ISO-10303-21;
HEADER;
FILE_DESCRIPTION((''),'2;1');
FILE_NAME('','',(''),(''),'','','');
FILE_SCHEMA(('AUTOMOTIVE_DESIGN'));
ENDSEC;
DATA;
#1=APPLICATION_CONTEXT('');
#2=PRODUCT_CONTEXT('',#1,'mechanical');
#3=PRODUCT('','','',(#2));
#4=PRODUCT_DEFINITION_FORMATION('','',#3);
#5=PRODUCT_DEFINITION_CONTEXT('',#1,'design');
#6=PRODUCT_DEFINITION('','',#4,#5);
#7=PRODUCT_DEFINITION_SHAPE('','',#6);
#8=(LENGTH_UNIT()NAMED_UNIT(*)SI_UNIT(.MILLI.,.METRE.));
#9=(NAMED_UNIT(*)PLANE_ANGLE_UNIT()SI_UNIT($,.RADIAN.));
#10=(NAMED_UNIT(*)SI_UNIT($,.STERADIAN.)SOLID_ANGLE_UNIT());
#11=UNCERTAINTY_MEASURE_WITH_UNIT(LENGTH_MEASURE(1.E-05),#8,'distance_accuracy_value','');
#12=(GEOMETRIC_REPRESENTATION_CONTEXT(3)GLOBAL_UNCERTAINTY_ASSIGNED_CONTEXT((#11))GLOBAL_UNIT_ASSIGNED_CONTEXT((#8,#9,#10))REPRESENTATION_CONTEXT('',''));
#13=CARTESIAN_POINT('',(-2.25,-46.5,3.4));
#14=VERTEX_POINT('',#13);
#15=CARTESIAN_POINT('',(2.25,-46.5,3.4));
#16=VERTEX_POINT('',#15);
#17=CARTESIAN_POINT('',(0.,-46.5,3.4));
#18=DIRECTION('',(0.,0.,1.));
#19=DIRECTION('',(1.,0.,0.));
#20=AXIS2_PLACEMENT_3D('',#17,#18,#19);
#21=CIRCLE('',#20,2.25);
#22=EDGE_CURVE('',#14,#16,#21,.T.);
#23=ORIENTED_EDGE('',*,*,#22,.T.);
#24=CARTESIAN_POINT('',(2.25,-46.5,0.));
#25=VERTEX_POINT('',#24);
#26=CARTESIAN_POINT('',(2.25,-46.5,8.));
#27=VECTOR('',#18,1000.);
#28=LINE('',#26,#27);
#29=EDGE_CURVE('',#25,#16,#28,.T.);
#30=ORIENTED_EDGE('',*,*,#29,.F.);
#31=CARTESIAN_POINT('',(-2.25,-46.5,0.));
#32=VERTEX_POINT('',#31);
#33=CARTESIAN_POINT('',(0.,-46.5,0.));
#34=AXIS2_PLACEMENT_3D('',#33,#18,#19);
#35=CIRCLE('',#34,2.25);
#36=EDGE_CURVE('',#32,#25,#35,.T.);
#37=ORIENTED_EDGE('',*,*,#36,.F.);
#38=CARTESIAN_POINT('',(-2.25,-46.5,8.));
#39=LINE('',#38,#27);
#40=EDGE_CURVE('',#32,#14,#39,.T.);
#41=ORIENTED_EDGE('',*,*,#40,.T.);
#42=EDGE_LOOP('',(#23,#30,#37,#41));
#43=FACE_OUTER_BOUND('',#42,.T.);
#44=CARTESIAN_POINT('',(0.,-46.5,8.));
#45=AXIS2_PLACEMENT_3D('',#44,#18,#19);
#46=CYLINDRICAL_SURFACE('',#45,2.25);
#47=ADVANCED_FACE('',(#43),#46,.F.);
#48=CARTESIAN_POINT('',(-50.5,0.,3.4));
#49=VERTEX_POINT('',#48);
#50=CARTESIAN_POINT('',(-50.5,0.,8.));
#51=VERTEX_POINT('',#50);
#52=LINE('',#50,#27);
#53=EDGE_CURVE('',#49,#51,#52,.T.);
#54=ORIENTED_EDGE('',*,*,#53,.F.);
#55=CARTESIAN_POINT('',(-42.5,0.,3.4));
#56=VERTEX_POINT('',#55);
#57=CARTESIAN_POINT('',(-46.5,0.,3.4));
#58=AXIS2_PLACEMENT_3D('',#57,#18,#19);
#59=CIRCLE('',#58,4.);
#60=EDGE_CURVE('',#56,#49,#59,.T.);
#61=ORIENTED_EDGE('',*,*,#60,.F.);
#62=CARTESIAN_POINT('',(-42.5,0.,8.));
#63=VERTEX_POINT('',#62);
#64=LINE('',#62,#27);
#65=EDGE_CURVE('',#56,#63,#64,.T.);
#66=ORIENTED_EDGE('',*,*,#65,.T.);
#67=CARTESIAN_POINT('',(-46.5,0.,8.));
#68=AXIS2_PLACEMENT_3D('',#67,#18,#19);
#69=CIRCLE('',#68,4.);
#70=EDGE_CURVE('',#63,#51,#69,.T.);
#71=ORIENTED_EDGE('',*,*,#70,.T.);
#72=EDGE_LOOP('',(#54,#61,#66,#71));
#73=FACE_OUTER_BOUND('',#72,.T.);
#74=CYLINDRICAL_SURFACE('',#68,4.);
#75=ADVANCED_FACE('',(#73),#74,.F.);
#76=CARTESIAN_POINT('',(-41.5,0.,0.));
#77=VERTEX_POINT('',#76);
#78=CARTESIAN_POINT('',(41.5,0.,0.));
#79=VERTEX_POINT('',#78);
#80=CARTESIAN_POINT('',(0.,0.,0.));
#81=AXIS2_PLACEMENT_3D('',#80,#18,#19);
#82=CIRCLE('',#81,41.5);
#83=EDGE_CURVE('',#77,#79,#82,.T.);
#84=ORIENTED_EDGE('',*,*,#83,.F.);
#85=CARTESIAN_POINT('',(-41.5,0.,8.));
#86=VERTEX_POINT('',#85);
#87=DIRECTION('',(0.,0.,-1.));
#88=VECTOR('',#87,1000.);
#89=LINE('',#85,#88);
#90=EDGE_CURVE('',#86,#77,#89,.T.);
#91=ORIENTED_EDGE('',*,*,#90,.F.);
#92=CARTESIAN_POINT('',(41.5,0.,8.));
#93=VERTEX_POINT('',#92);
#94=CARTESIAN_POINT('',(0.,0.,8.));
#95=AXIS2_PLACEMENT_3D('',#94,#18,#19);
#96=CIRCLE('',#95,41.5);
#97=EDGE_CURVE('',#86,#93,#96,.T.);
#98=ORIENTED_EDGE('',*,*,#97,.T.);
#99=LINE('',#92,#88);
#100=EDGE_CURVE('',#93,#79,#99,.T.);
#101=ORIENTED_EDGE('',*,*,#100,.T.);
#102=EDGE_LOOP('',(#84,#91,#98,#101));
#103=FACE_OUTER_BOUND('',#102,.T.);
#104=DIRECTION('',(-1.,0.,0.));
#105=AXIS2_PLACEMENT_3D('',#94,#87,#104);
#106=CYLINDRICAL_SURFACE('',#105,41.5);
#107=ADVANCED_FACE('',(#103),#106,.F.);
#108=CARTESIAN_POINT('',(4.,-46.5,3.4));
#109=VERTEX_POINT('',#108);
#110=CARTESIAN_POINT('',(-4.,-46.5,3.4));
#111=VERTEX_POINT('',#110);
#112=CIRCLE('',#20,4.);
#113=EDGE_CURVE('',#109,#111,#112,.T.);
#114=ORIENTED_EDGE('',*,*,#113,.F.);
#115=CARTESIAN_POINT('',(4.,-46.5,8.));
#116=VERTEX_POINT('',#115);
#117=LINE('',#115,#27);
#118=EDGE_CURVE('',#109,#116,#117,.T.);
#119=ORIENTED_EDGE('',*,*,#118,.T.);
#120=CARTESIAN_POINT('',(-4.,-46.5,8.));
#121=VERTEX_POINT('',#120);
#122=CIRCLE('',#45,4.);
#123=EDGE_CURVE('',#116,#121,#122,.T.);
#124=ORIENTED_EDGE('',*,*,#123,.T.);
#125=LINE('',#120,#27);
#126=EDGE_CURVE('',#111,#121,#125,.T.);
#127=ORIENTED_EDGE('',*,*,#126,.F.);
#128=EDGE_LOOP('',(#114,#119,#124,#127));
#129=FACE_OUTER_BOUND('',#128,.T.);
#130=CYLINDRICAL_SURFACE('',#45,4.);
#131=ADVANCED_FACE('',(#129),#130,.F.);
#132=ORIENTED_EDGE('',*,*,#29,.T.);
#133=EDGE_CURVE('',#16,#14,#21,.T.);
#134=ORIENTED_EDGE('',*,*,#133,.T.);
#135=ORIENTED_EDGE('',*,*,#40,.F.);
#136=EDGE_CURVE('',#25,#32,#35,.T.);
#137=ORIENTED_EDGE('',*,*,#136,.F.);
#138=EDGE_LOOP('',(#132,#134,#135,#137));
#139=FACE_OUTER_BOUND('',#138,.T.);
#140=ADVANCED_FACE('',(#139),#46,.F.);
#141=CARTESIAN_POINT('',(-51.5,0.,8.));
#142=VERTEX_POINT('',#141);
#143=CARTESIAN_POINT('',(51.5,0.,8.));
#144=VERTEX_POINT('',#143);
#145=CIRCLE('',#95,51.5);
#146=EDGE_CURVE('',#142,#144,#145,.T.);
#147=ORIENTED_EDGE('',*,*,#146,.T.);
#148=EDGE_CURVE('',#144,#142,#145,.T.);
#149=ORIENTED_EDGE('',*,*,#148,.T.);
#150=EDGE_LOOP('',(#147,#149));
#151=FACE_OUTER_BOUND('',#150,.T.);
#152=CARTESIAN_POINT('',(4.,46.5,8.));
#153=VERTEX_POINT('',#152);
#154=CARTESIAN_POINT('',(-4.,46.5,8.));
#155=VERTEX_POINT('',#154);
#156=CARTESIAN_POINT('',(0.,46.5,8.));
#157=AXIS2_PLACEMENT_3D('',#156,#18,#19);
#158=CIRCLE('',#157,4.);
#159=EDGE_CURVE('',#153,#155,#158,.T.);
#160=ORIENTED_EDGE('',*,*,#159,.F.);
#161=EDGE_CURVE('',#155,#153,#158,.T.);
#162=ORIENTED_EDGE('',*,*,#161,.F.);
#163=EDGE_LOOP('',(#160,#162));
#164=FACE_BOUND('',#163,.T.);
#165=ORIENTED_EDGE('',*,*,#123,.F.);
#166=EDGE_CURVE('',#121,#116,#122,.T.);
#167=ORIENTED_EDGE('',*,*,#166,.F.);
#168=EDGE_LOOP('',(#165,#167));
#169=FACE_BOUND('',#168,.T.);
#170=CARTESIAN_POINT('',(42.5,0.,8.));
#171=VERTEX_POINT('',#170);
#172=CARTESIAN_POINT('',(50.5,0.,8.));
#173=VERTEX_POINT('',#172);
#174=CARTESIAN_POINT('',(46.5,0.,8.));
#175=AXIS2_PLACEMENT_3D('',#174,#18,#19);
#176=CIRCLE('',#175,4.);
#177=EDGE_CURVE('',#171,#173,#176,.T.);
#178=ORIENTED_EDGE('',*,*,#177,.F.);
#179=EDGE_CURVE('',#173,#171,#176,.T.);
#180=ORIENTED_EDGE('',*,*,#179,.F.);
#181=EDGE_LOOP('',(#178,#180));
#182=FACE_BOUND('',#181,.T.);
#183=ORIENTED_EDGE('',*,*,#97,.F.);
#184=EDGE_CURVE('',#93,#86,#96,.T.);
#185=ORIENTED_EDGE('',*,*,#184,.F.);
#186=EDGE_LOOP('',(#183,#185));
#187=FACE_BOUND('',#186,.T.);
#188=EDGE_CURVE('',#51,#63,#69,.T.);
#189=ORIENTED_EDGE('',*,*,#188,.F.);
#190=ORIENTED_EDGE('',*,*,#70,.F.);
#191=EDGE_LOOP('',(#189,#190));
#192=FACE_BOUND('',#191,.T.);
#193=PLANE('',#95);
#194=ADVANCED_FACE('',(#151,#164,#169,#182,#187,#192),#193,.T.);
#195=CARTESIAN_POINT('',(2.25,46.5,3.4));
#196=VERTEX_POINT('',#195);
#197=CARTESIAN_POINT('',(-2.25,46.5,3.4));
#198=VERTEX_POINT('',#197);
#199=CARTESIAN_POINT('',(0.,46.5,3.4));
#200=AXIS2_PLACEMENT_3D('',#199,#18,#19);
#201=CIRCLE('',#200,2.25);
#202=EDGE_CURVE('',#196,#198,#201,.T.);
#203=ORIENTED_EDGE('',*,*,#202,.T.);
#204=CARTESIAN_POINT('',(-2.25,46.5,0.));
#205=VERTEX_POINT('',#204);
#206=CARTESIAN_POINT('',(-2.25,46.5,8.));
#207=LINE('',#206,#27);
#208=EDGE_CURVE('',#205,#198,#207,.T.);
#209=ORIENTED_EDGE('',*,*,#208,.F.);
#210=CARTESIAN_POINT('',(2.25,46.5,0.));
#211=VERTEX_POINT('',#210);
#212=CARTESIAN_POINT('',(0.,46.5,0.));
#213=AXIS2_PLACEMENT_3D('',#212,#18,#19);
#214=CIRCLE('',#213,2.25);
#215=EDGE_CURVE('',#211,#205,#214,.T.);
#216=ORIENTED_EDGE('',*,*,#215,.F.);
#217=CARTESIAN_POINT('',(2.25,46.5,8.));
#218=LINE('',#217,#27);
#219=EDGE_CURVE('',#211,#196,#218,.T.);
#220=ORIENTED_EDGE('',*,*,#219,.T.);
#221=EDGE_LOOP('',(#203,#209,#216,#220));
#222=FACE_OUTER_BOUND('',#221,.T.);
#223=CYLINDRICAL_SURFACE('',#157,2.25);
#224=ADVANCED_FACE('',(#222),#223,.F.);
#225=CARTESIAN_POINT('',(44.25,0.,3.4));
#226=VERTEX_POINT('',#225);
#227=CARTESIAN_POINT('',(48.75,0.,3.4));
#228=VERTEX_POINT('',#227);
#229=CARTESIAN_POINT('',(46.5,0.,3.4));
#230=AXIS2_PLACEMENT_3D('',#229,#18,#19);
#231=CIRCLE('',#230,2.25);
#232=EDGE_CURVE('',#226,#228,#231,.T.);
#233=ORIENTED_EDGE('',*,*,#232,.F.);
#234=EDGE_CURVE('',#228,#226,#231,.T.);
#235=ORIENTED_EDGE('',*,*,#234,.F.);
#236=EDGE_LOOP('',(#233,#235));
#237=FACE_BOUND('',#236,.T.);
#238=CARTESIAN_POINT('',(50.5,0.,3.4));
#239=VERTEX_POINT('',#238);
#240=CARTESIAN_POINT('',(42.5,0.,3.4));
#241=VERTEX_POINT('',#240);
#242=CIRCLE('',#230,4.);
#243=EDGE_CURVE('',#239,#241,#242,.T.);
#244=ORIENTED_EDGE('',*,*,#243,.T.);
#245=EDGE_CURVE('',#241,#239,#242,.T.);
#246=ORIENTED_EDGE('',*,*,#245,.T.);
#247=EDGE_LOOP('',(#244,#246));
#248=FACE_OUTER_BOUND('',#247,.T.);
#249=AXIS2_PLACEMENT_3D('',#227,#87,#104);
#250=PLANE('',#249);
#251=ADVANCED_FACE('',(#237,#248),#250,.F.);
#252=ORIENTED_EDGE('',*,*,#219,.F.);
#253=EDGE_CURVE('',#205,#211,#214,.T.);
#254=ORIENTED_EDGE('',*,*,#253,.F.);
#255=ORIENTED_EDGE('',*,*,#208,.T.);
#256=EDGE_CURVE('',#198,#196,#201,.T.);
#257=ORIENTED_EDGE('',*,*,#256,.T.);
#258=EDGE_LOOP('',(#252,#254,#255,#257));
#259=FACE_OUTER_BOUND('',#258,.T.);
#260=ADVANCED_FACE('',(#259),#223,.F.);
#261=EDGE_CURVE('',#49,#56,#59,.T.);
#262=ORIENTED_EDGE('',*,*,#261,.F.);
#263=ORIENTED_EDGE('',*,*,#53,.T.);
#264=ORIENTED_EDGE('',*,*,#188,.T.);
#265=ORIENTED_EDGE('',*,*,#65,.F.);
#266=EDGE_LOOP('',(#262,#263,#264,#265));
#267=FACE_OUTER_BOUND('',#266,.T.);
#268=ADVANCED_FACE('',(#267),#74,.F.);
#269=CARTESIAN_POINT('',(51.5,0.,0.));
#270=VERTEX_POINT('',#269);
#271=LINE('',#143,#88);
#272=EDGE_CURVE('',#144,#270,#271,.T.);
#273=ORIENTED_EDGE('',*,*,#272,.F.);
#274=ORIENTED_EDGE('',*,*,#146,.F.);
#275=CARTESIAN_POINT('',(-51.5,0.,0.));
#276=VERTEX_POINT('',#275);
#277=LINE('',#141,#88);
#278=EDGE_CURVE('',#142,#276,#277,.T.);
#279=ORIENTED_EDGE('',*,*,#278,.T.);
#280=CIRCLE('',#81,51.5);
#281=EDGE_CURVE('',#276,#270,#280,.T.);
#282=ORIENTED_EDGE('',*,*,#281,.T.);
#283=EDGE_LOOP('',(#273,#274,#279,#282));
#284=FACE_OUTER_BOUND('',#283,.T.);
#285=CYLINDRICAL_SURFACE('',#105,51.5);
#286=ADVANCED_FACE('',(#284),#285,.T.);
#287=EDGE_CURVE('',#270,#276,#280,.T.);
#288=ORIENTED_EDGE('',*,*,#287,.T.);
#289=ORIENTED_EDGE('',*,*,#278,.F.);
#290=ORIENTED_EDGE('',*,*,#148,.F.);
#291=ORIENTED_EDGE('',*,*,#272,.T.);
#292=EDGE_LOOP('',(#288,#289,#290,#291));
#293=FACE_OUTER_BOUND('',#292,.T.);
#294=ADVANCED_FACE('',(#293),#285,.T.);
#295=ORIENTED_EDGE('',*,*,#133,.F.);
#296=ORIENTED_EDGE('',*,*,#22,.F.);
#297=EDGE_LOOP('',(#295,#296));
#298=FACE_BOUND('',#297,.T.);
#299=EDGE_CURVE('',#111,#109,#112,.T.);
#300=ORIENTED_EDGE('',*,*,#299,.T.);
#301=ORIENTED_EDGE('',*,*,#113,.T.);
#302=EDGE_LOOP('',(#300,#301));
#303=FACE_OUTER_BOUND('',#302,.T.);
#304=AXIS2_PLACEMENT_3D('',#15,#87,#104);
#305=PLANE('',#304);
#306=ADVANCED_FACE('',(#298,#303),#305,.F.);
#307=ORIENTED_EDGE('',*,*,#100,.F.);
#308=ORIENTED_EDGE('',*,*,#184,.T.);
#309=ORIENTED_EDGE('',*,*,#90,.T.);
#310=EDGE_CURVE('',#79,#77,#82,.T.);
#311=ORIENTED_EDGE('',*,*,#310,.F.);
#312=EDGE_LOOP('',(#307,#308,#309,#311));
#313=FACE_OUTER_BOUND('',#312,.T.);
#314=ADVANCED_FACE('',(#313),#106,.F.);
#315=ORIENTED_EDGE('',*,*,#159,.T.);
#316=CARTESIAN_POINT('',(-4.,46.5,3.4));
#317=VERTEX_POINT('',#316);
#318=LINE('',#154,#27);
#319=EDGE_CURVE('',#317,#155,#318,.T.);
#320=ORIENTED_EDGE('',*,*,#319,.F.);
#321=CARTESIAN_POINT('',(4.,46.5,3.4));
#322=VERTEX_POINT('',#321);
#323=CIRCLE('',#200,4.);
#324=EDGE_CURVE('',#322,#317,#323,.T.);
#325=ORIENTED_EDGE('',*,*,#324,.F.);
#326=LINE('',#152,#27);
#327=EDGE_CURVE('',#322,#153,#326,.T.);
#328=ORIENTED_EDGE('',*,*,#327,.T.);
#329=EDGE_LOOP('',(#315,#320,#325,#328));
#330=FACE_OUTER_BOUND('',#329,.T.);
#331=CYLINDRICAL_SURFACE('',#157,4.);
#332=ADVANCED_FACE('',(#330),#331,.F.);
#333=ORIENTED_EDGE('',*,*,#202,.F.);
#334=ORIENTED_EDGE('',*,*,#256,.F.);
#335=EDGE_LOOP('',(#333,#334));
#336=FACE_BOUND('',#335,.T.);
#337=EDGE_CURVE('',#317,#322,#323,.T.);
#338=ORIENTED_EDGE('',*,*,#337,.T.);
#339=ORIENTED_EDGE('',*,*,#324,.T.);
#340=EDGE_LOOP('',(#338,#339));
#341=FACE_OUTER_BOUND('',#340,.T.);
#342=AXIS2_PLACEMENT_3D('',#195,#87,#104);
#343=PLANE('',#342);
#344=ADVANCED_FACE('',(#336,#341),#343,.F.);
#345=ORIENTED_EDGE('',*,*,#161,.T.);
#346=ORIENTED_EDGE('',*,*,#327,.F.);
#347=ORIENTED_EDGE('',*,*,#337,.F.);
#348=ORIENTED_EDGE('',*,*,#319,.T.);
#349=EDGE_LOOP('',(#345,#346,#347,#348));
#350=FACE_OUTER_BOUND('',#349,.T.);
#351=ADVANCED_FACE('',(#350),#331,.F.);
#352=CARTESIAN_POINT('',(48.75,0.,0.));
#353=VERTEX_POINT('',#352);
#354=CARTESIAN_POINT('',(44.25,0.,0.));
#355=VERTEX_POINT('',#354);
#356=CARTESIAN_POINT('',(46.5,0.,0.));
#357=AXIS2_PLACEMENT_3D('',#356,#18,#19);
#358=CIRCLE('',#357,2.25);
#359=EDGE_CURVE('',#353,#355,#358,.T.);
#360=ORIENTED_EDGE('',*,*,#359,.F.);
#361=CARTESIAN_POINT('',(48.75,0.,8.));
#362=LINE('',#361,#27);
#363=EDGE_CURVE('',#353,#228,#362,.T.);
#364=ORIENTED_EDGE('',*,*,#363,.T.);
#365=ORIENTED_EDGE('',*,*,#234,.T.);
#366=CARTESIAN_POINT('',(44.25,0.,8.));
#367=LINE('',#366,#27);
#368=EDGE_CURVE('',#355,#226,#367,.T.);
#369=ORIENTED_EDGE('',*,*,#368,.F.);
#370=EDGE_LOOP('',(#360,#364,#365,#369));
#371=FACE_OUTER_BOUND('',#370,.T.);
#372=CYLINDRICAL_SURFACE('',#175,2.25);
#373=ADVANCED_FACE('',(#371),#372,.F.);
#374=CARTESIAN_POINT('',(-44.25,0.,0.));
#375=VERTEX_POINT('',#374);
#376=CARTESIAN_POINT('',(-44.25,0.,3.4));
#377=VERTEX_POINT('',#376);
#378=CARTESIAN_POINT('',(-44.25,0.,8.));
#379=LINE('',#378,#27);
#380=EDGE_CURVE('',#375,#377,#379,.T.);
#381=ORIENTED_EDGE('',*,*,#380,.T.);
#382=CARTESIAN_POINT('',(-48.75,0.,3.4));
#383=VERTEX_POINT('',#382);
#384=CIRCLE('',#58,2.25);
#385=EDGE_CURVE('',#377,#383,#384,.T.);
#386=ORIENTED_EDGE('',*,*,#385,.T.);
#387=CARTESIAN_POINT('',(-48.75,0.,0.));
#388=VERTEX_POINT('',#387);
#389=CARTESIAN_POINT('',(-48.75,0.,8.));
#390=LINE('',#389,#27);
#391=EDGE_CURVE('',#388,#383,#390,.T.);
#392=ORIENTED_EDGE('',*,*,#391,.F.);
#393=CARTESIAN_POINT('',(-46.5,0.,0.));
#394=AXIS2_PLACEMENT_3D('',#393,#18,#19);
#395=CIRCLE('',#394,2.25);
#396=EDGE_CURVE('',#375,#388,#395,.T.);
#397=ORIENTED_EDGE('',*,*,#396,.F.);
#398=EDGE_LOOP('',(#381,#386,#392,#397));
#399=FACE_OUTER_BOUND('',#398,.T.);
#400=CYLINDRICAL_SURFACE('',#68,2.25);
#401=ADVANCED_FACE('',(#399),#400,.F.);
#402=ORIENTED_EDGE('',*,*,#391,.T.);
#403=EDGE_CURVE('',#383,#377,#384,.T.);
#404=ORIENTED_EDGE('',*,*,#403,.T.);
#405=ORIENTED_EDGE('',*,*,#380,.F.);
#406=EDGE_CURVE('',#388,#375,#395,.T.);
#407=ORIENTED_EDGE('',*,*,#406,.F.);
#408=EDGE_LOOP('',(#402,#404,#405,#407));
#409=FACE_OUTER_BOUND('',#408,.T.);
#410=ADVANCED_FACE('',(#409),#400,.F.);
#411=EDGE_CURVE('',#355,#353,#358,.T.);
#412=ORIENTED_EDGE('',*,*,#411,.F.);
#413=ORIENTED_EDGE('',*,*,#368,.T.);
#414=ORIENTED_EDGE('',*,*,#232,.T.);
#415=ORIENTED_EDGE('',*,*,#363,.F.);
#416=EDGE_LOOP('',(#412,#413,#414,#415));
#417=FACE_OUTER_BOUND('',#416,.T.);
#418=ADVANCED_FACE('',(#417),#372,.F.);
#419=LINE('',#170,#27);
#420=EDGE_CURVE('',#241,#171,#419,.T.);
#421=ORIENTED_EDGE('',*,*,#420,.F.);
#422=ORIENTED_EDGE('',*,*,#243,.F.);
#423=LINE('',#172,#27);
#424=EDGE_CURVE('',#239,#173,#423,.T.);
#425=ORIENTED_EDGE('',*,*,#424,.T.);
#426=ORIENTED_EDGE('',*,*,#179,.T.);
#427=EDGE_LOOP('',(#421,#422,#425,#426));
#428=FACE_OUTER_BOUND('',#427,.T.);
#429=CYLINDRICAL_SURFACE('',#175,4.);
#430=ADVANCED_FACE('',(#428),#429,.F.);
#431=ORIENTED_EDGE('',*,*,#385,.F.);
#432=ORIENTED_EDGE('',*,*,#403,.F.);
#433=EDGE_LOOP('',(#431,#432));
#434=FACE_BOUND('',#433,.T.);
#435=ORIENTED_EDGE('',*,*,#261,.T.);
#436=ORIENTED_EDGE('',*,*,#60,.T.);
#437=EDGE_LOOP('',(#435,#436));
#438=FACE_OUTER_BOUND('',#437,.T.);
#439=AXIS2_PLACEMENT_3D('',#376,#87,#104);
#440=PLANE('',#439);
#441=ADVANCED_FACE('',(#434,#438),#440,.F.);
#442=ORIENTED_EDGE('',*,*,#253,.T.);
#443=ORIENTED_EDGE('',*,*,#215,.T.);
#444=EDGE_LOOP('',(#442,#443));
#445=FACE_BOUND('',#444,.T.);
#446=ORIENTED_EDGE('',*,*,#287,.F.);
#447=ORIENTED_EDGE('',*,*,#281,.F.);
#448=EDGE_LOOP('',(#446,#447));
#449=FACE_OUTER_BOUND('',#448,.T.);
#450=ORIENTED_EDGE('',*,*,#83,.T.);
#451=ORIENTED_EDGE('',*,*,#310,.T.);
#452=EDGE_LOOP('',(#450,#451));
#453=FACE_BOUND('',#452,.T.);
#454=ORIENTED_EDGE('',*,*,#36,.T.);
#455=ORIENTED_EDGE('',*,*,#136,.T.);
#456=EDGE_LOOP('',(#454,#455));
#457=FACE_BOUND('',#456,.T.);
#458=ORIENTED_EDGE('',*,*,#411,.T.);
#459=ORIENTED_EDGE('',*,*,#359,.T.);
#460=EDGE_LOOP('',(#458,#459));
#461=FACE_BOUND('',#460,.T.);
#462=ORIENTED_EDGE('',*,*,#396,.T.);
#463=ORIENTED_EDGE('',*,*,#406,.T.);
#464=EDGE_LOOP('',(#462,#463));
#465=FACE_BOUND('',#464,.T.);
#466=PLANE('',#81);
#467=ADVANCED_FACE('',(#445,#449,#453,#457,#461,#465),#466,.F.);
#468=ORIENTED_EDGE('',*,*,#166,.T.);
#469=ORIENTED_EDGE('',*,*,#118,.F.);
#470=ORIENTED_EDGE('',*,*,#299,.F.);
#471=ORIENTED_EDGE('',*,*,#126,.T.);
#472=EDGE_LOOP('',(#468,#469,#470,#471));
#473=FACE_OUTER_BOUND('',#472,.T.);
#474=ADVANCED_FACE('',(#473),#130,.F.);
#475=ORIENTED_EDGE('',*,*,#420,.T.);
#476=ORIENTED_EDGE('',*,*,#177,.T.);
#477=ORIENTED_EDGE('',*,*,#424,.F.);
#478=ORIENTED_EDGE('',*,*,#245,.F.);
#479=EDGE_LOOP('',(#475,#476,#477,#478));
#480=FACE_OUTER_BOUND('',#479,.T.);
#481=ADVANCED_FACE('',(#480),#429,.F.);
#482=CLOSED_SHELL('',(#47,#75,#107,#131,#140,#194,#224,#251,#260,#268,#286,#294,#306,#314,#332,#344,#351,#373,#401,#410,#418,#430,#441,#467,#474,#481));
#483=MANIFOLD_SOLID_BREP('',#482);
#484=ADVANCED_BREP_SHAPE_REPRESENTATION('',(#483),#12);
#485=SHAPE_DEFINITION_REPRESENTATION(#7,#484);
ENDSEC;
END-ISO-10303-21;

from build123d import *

# Parameters (mm, degrees)
SKETCH1_R           = 51.5
SKETCH1_R_2         = 41.5
BOSS_EXTRUDE1_DEPTH = 8
CIRPATTERN1_COUNT   = 4


with BuildPart() as part:
    # Sketch1 → Boss-Extrude1 (new body)
    with BuildSketch(Plane.XY):
        Circle(SKETCH1_R)
        Circle(SKETCH1_R_2, mode=Mode.SUBTRACT)
    extrude(amount=BOSS_EXTRUDE1_DEPTH)

    # Sketch5 → Hole size per hex socket cap screw type1 (revolve, cut)
    with BuildSketch(Plane(origin=(0, 46.5, 8), x_dir=(0, -1, 0), z_dir=(1, 0, 0))):
        Polygon((0, 0), (0, 18.351936393), (2.25, 17), (2.25, 4.6), (4, 4.6), (4, 0), align=None)
    hole_size_per_hex_socket_cap_screw_type1 = revolve(axis=Axis((0, 46.5, 14.35), (0, 0, -1)), mode=Mode.SUBTRACT)

    # CirPattern1: Hole size per hex socket cap screw type1 ×4 about axis
    cirpattern1_axis = Axis((0, 0, 0), (0, 0, 1))
    for i in range(1, CIRPATTERN1_COUNT):
        add(hole_size_per_hex_socket_cap_screw_type1.rotate(cirpattern1_axis, i * 360 / CIRPATTERN1_COUNT), mode=Mode.SUBTRACT)


solid = part.part
